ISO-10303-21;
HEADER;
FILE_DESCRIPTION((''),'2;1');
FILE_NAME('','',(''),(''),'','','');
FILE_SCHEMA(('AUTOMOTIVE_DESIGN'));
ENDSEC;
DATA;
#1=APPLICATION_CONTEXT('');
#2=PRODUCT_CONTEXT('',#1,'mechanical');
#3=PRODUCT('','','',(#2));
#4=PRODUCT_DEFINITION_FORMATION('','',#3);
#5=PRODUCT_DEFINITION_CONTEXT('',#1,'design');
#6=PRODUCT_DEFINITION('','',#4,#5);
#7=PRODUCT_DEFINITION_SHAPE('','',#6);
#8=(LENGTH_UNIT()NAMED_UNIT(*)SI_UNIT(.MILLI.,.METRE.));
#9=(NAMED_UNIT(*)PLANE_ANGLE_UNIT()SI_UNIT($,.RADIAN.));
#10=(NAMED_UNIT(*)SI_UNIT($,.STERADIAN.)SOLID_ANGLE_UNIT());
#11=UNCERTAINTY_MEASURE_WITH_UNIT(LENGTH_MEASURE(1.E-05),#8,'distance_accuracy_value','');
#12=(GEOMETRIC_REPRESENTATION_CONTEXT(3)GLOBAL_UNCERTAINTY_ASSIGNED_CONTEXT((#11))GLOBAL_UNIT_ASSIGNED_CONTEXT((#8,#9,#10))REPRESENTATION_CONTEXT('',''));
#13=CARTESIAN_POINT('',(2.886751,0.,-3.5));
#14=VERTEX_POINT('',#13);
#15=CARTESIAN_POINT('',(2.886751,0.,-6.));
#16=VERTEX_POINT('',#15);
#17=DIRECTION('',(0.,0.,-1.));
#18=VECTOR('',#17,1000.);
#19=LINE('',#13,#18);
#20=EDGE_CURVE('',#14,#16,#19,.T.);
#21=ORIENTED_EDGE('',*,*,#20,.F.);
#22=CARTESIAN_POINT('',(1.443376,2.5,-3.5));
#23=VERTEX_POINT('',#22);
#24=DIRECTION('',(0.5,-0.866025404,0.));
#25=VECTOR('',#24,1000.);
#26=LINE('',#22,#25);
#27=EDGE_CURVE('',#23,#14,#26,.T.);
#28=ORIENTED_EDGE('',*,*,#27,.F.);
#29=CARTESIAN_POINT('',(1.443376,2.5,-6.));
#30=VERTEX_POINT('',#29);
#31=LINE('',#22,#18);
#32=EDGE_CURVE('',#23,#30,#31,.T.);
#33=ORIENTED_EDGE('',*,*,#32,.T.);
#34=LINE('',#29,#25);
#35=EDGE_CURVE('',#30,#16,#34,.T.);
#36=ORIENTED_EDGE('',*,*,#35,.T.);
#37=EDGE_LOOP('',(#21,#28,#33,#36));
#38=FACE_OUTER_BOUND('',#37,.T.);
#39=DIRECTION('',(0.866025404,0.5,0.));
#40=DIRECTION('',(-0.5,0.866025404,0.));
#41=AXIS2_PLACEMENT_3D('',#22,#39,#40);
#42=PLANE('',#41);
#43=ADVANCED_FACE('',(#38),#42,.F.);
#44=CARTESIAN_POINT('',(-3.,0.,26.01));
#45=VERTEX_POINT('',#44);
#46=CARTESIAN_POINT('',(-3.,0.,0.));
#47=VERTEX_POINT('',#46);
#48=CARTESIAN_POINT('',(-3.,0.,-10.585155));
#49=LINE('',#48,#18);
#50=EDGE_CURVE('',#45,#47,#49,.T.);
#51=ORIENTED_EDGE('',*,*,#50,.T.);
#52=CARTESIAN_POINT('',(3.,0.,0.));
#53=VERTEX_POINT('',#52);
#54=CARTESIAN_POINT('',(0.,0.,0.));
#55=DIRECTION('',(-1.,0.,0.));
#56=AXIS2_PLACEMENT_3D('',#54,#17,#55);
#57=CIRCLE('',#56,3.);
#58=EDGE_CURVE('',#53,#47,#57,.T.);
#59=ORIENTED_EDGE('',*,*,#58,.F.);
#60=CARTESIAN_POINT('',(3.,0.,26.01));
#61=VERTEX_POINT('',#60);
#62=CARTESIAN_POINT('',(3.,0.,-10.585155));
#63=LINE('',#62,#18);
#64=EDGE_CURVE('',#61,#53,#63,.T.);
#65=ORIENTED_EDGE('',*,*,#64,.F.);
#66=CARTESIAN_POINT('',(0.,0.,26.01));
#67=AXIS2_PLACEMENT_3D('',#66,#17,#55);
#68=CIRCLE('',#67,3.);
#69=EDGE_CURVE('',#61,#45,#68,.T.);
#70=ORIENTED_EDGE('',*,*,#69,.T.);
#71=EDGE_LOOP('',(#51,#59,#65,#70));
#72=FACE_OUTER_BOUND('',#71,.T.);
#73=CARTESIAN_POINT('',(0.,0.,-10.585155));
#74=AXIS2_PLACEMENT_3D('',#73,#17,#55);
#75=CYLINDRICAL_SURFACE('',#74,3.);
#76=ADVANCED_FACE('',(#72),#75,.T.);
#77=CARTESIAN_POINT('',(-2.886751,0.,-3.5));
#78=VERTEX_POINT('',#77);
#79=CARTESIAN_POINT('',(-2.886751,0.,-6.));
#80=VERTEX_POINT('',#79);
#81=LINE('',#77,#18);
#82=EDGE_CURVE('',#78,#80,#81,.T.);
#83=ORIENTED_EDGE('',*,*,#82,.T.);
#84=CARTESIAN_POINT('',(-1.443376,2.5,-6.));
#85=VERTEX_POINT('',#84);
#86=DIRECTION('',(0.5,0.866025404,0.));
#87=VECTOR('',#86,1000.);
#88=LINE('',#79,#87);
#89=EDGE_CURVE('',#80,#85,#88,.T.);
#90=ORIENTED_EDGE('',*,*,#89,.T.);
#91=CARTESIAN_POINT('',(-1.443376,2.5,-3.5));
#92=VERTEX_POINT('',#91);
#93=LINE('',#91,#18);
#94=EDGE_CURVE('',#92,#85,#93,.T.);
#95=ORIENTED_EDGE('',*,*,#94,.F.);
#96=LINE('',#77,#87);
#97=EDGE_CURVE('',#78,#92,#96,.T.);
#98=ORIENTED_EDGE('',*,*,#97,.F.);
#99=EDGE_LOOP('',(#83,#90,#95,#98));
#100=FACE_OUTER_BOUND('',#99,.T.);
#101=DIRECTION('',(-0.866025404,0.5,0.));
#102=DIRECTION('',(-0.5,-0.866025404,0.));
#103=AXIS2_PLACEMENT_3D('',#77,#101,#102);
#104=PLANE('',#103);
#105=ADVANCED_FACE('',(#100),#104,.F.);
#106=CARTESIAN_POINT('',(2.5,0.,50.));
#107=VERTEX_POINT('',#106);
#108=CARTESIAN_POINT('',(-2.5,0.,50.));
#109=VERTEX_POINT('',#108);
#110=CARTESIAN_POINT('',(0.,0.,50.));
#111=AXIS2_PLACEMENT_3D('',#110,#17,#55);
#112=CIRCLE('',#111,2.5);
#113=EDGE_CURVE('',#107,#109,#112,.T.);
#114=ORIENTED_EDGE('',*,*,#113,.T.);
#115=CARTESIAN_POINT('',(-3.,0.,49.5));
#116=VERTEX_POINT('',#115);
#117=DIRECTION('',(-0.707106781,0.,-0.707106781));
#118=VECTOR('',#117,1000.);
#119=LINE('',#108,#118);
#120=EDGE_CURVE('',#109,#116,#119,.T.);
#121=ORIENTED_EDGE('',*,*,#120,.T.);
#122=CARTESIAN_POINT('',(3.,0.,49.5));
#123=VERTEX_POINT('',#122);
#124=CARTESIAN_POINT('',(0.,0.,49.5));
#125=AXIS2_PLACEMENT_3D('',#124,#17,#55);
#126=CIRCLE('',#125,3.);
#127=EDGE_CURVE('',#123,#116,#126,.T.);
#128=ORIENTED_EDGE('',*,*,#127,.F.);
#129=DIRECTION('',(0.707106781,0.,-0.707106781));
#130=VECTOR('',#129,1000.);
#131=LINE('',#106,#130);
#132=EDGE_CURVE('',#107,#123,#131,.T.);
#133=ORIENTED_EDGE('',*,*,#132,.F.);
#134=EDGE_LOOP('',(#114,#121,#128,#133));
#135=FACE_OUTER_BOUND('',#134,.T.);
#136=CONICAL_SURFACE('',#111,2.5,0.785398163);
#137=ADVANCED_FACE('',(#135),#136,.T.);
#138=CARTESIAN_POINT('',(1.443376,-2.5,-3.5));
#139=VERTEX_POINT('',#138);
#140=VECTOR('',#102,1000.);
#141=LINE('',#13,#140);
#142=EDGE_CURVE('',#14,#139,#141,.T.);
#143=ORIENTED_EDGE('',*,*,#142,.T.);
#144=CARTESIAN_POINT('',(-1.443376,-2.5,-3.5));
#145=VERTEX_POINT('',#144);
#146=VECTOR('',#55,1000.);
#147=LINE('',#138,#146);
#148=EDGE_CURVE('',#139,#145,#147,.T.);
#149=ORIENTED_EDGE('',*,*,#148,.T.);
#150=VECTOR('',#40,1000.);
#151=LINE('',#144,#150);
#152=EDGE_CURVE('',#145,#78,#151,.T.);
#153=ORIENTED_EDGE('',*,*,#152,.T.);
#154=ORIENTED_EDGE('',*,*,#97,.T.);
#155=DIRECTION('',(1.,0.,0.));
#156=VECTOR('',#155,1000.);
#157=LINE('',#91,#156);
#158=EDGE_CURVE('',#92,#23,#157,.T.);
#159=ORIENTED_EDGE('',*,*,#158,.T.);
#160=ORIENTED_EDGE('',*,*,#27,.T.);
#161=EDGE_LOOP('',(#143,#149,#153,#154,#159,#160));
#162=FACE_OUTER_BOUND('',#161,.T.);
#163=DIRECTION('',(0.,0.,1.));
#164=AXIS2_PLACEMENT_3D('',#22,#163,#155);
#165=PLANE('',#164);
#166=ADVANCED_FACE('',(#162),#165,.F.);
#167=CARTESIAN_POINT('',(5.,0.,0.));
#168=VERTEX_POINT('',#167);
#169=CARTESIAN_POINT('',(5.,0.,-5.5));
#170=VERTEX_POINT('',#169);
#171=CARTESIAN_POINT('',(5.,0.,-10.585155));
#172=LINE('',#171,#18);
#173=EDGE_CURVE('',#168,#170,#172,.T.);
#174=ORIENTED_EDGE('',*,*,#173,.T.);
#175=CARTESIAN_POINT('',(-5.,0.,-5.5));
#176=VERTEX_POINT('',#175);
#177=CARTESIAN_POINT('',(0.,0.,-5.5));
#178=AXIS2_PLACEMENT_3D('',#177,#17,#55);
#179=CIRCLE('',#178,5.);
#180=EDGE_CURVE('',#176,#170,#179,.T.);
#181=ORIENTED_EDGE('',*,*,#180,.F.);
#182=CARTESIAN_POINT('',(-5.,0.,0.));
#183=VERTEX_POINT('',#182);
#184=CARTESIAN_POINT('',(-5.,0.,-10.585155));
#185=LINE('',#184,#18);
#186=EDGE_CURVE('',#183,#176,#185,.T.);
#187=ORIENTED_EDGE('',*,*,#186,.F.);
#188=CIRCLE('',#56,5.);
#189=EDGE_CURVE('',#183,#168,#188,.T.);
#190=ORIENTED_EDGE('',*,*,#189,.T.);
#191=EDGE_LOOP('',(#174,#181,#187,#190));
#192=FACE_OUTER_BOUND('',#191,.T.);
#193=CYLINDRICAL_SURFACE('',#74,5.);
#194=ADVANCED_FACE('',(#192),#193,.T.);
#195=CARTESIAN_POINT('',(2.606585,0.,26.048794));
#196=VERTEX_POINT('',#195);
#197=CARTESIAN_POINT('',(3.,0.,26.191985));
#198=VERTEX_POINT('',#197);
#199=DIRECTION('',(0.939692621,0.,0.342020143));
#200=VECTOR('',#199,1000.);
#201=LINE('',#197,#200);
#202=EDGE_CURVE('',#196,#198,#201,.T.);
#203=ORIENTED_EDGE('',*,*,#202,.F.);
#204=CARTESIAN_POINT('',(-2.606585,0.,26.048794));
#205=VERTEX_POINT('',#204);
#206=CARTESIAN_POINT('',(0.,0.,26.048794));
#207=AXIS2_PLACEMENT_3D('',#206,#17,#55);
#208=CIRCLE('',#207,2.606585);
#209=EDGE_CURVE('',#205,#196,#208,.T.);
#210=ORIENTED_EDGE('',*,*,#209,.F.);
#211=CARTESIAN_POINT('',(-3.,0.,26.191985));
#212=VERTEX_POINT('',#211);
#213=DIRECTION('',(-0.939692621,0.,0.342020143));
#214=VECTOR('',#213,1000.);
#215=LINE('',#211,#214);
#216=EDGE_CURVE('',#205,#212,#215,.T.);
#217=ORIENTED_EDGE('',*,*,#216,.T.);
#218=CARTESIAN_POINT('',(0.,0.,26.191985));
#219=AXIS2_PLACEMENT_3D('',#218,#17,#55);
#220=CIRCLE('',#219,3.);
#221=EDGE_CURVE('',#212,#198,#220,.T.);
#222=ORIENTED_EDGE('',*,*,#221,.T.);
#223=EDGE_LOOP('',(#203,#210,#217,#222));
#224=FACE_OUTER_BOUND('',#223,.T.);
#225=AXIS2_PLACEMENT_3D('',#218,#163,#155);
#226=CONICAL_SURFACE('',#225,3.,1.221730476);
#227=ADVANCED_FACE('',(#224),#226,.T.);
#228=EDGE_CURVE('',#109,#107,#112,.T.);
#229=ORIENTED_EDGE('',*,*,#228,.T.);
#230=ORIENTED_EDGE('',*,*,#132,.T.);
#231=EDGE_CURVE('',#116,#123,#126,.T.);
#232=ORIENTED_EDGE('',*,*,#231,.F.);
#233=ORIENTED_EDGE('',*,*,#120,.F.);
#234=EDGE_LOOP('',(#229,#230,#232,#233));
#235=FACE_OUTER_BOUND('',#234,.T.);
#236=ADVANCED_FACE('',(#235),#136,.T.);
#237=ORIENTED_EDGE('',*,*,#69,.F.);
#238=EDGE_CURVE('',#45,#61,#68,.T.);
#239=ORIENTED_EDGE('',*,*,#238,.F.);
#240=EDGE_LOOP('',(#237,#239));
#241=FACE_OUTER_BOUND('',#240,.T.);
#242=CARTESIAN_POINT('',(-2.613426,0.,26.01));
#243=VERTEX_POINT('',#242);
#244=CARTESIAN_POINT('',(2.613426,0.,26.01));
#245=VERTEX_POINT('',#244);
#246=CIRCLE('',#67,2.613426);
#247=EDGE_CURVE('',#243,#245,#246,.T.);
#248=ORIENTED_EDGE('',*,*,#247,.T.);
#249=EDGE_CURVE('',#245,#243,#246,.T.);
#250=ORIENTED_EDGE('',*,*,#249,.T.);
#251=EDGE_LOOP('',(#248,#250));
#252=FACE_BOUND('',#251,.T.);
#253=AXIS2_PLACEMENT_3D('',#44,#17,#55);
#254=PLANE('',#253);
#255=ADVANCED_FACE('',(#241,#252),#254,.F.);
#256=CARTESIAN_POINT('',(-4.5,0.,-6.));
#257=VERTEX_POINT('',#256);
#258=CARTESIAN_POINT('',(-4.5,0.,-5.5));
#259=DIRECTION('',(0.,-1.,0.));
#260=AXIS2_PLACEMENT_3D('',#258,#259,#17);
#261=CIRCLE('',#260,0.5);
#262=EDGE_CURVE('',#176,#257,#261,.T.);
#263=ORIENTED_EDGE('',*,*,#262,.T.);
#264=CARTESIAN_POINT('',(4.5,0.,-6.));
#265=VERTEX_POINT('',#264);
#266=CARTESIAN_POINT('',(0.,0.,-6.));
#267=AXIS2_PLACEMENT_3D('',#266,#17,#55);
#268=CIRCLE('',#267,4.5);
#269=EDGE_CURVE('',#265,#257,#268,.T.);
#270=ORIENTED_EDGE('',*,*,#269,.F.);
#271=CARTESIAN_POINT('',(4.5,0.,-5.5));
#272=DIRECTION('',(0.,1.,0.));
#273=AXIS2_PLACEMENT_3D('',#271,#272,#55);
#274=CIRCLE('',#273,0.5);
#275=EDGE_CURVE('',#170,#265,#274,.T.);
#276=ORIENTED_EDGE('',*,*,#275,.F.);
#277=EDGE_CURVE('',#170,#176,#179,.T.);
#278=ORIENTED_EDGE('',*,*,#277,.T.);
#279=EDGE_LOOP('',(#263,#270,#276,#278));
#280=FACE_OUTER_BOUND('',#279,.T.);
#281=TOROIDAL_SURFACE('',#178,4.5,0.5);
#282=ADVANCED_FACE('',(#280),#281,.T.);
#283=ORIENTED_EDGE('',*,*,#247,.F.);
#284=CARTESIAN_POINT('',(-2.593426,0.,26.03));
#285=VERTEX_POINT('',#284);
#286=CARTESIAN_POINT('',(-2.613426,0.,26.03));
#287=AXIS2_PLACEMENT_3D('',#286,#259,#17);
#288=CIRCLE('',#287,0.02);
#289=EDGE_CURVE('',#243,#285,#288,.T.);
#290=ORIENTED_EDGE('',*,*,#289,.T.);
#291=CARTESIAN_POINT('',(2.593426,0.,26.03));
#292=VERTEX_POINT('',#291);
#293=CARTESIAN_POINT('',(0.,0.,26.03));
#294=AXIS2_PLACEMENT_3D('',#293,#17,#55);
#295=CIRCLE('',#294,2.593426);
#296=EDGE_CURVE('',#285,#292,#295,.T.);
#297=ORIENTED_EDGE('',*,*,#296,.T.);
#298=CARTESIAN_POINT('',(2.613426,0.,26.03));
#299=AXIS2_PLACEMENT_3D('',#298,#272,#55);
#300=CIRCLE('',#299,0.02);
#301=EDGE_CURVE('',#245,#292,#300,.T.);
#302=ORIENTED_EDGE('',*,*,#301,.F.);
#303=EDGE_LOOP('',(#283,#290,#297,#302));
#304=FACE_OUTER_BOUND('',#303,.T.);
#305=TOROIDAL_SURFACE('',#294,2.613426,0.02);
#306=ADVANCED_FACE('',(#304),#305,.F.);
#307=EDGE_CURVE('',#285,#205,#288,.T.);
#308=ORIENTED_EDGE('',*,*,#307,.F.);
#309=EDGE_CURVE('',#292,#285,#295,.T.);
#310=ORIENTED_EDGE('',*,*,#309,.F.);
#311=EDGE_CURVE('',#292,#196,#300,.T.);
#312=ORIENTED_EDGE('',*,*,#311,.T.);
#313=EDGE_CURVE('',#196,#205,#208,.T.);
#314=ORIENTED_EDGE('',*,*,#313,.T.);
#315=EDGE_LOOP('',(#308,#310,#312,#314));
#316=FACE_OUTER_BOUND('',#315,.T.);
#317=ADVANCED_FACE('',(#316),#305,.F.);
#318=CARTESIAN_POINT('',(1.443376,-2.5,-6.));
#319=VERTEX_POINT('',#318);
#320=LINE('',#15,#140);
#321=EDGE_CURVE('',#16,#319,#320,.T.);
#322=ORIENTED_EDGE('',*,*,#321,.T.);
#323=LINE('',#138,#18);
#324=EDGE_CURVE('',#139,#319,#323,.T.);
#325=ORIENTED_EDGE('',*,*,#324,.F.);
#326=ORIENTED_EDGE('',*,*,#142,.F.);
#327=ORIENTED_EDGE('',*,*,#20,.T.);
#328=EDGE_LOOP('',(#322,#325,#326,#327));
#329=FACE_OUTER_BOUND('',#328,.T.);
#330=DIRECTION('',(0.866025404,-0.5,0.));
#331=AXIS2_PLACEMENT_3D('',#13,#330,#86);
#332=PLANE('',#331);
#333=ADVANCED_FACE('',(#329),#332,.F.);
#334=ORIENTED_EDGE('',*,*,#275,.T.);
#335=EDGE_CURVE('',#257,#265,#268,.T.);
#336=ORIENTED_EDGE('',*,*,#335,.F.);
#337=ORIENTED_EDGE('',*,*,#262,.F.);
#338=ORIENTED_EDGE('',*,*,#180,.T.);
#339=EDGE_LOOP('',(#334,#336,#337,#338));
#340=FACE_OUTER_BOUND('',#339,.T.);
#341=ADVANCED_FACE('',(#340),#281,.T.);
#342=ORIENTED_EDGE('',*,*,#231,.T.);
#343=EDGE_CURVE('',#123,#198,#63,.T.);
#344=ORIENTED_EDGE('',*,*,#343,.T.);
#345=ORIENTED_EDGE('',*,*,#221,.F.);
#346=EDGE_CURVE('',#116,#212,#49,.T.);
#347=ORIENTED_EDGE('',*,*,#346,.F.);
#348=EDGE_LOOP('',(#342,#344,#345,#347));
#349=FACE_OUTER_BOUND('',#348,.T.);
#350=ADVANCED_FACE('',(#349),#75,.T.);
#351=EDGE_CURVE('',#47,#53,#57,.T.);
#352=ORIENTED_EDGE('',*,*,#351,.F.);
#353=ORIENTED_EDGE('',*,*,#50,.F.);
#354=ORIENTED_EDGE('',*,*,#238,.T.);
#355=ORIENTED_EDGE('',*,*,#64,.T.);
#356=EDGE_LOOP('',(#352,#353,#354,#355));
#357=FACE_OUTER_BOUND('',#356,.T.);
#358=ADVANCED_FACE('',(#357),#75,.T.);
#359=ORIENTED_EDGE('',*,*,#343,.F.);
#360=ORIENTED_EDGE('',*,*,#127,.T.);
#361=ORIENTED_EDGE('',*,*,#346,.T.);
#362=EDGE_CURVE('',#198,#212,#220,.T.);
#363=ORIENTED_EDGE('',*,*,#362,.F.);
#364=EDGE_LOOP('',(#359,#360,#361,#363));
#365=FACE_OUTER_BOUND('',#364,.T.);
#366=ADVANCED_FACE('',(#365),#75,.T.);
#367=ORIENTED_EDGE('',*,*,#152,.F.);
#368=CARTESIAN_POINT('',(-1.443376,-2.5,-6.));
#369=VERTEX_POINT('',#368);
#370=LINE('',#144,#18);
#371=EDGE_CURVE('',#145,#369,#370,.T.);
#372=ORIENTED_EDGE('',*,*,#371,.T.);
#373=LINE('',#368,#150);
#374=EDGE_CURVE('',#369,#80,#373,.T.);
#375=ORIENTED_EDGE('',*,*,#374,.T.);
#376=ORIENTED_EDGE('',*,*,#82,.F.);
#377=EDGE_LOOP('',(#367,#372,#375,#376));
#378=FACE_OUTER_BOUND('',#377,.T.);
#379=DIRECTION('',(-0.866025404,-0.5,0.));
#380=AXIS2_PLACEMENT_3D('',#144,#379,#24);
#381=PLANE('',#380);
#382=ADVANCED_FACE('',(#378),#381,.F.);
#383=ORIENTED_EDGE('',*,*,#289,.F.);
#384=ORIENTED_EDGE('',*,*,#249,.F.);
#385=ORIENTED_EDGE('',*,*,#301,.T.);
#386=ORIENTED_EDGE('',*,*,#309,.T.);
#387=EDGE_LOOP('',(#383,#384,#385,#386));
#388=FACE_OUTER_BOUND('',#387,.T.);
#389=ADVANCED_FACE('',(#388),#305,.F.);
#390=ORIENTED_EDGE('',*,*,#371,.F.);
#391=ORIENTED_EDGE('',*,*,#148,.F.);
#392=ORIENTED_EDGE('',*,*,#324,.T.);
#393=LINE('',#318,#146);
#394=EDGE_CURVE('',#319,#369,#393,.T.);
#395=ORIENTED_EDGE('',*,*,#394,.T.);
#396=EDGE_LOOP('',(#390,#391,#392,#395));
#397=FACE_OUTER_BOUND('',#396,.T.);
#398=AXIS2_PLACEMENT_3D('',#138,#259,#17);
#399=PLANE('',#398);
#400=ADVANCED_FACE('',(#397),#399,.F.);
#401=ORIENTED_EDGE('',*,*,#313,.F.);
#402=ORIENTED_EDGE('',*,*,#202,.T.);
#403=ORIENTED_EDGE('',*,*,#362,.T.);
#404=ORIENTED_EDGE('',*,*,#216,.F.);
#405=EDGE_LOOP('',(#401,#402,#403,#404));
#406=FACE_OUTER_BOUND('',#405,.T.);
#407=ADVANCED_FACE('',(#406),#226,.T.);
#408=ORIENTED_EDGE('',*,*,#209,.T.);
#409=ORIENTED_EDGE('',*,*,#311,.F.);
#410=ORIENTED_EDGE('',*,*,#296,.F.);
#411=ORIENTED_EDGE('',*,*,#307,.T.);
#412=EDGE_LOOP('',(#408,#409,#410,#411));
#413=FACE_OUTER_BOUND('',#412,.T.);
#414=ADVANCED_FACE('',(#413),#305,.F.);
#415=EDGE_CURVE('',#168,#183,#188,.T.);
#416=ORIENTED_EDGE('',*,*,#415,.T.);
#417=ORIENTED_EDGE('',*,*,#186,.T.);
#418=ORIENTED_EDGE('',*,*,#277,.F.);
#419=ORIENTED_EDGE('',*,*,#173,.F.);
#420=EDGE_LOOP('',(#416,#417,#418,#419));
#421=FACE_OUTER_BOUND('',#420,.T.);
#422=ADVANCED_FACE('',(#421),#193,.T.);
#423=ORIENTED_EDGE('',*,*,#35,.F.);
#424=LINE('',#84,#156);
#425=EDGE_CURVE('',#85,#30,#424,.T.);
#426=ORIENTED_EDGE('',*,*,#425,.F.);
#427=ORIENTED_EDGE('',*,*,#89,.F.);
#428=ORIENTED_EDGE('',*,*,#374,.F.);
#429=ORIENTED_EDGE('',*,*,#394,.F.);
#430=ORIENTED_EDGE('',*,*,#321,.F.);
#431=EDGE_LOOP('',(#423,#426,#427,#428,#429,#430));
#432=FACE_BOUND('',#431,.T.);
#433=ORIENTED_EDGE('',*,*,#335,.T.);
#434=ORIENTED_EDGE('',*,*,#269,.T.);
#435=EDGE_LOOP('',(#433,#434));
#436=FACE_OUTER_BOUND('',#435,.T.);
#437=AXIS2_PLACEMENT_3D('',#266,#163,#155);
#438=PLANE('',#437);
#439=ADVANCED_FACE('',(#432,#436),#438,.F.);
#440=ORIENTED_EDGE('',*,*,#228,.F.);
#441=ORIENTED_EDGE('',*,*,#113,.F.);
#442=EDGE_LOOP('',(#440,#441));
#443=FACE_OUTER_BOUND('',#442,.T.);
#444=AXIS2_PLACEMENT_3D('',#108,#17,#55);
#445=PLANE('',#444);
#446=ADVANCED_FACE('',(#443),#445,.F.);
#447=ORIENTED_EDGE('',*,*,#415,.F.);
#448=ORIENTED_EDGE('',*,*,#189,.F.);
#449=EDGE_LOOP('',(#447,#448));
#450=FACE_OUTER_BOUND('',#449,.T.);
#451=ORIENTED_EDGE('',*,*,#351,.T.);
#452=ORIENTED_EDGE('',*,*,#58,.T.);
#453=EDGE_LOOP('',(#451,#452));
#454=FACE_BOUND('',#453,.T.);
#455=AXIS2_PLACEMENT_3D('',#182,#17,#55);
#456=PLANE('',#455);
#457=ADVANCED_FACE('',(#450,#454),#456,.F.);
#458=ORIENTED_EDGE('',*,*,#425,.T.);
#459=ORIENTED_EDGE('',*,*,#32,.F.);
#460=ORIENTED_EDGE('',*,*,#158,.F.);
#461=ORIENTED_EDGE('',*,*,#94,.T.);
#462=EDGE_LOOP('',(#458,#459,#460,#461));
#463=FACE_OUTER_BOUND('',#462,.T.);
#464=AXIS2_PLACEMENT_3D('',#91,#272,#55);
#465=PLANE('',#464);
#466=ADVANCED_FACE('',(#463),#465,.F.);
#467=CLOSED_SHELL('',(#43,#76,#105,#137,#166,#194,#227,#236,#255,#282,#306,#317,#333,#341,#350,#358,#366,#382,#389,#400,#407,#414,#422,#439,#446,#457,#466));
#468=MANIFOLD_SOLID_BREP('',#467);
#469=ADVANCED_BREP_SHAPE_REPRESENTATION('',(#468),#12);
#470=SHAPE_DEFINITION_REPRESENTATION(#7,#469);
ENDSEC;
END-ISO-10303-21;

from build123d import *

# Parameters (mm, degrees)
CUT_EXTRUDE1_DEPTH = 2.5


with BuildPart() as part:
    # Logo3_bib1 → Revolve1 (revolve)
    with BuildSketch(Plane(origin=(0, 0, 0), x_dir=(-1, 0, 0), z_dir=(0, -1, 0))):
        with BuildLine():
            Line((0, -50), (0, 6))
            Line((0, 6), (4.5, 6))
            ThreePointArc((4.5, 6), (4.853553391, 5.853553391), (5, 5.5))
            Line((5, 5.5), (5, 0))
            Line((5, 0), (3, 0))
            Line((3, 0), (3, -26.01))
            Line((3, -26.01), (2.613425636, -26.01))
            ThreePointArc((2.613425636, -26.01), (2.593729481, -26.026527036), (2.606585234, -26.048793852))
            Line((2.606585234, -26.048793852), (3, -26.191985117))
            Line((3, -26.191985117), (3, -49.5))
            Line((3, -49.5), (2.5, -50))
            Line((2.5, -50), (0, -50))
        make_face()
    revolve(axis=Axis((0, 0, -10.585154653), (0, 0, 1)))

    # Logo3_bib2 → Cut-Extrude1 (cut)
    with BuildSketch(Plane(origin=(0, 0, -6), x_dir=(1, 0, 0), z_dir=(0, 0, -1))):
        Polygon((2.886751346, 0), (1.443375673, 2.5), (-1.443375673, 2.5), (-2.886751346, 0), (-1.443375673, -2.5), (1.443375673, -2.5), align=None)
    extrude(amount=-CUT_EXTRUDE1_DEPTH, mode=Mode.SUBTRACT)


solid = part.part
